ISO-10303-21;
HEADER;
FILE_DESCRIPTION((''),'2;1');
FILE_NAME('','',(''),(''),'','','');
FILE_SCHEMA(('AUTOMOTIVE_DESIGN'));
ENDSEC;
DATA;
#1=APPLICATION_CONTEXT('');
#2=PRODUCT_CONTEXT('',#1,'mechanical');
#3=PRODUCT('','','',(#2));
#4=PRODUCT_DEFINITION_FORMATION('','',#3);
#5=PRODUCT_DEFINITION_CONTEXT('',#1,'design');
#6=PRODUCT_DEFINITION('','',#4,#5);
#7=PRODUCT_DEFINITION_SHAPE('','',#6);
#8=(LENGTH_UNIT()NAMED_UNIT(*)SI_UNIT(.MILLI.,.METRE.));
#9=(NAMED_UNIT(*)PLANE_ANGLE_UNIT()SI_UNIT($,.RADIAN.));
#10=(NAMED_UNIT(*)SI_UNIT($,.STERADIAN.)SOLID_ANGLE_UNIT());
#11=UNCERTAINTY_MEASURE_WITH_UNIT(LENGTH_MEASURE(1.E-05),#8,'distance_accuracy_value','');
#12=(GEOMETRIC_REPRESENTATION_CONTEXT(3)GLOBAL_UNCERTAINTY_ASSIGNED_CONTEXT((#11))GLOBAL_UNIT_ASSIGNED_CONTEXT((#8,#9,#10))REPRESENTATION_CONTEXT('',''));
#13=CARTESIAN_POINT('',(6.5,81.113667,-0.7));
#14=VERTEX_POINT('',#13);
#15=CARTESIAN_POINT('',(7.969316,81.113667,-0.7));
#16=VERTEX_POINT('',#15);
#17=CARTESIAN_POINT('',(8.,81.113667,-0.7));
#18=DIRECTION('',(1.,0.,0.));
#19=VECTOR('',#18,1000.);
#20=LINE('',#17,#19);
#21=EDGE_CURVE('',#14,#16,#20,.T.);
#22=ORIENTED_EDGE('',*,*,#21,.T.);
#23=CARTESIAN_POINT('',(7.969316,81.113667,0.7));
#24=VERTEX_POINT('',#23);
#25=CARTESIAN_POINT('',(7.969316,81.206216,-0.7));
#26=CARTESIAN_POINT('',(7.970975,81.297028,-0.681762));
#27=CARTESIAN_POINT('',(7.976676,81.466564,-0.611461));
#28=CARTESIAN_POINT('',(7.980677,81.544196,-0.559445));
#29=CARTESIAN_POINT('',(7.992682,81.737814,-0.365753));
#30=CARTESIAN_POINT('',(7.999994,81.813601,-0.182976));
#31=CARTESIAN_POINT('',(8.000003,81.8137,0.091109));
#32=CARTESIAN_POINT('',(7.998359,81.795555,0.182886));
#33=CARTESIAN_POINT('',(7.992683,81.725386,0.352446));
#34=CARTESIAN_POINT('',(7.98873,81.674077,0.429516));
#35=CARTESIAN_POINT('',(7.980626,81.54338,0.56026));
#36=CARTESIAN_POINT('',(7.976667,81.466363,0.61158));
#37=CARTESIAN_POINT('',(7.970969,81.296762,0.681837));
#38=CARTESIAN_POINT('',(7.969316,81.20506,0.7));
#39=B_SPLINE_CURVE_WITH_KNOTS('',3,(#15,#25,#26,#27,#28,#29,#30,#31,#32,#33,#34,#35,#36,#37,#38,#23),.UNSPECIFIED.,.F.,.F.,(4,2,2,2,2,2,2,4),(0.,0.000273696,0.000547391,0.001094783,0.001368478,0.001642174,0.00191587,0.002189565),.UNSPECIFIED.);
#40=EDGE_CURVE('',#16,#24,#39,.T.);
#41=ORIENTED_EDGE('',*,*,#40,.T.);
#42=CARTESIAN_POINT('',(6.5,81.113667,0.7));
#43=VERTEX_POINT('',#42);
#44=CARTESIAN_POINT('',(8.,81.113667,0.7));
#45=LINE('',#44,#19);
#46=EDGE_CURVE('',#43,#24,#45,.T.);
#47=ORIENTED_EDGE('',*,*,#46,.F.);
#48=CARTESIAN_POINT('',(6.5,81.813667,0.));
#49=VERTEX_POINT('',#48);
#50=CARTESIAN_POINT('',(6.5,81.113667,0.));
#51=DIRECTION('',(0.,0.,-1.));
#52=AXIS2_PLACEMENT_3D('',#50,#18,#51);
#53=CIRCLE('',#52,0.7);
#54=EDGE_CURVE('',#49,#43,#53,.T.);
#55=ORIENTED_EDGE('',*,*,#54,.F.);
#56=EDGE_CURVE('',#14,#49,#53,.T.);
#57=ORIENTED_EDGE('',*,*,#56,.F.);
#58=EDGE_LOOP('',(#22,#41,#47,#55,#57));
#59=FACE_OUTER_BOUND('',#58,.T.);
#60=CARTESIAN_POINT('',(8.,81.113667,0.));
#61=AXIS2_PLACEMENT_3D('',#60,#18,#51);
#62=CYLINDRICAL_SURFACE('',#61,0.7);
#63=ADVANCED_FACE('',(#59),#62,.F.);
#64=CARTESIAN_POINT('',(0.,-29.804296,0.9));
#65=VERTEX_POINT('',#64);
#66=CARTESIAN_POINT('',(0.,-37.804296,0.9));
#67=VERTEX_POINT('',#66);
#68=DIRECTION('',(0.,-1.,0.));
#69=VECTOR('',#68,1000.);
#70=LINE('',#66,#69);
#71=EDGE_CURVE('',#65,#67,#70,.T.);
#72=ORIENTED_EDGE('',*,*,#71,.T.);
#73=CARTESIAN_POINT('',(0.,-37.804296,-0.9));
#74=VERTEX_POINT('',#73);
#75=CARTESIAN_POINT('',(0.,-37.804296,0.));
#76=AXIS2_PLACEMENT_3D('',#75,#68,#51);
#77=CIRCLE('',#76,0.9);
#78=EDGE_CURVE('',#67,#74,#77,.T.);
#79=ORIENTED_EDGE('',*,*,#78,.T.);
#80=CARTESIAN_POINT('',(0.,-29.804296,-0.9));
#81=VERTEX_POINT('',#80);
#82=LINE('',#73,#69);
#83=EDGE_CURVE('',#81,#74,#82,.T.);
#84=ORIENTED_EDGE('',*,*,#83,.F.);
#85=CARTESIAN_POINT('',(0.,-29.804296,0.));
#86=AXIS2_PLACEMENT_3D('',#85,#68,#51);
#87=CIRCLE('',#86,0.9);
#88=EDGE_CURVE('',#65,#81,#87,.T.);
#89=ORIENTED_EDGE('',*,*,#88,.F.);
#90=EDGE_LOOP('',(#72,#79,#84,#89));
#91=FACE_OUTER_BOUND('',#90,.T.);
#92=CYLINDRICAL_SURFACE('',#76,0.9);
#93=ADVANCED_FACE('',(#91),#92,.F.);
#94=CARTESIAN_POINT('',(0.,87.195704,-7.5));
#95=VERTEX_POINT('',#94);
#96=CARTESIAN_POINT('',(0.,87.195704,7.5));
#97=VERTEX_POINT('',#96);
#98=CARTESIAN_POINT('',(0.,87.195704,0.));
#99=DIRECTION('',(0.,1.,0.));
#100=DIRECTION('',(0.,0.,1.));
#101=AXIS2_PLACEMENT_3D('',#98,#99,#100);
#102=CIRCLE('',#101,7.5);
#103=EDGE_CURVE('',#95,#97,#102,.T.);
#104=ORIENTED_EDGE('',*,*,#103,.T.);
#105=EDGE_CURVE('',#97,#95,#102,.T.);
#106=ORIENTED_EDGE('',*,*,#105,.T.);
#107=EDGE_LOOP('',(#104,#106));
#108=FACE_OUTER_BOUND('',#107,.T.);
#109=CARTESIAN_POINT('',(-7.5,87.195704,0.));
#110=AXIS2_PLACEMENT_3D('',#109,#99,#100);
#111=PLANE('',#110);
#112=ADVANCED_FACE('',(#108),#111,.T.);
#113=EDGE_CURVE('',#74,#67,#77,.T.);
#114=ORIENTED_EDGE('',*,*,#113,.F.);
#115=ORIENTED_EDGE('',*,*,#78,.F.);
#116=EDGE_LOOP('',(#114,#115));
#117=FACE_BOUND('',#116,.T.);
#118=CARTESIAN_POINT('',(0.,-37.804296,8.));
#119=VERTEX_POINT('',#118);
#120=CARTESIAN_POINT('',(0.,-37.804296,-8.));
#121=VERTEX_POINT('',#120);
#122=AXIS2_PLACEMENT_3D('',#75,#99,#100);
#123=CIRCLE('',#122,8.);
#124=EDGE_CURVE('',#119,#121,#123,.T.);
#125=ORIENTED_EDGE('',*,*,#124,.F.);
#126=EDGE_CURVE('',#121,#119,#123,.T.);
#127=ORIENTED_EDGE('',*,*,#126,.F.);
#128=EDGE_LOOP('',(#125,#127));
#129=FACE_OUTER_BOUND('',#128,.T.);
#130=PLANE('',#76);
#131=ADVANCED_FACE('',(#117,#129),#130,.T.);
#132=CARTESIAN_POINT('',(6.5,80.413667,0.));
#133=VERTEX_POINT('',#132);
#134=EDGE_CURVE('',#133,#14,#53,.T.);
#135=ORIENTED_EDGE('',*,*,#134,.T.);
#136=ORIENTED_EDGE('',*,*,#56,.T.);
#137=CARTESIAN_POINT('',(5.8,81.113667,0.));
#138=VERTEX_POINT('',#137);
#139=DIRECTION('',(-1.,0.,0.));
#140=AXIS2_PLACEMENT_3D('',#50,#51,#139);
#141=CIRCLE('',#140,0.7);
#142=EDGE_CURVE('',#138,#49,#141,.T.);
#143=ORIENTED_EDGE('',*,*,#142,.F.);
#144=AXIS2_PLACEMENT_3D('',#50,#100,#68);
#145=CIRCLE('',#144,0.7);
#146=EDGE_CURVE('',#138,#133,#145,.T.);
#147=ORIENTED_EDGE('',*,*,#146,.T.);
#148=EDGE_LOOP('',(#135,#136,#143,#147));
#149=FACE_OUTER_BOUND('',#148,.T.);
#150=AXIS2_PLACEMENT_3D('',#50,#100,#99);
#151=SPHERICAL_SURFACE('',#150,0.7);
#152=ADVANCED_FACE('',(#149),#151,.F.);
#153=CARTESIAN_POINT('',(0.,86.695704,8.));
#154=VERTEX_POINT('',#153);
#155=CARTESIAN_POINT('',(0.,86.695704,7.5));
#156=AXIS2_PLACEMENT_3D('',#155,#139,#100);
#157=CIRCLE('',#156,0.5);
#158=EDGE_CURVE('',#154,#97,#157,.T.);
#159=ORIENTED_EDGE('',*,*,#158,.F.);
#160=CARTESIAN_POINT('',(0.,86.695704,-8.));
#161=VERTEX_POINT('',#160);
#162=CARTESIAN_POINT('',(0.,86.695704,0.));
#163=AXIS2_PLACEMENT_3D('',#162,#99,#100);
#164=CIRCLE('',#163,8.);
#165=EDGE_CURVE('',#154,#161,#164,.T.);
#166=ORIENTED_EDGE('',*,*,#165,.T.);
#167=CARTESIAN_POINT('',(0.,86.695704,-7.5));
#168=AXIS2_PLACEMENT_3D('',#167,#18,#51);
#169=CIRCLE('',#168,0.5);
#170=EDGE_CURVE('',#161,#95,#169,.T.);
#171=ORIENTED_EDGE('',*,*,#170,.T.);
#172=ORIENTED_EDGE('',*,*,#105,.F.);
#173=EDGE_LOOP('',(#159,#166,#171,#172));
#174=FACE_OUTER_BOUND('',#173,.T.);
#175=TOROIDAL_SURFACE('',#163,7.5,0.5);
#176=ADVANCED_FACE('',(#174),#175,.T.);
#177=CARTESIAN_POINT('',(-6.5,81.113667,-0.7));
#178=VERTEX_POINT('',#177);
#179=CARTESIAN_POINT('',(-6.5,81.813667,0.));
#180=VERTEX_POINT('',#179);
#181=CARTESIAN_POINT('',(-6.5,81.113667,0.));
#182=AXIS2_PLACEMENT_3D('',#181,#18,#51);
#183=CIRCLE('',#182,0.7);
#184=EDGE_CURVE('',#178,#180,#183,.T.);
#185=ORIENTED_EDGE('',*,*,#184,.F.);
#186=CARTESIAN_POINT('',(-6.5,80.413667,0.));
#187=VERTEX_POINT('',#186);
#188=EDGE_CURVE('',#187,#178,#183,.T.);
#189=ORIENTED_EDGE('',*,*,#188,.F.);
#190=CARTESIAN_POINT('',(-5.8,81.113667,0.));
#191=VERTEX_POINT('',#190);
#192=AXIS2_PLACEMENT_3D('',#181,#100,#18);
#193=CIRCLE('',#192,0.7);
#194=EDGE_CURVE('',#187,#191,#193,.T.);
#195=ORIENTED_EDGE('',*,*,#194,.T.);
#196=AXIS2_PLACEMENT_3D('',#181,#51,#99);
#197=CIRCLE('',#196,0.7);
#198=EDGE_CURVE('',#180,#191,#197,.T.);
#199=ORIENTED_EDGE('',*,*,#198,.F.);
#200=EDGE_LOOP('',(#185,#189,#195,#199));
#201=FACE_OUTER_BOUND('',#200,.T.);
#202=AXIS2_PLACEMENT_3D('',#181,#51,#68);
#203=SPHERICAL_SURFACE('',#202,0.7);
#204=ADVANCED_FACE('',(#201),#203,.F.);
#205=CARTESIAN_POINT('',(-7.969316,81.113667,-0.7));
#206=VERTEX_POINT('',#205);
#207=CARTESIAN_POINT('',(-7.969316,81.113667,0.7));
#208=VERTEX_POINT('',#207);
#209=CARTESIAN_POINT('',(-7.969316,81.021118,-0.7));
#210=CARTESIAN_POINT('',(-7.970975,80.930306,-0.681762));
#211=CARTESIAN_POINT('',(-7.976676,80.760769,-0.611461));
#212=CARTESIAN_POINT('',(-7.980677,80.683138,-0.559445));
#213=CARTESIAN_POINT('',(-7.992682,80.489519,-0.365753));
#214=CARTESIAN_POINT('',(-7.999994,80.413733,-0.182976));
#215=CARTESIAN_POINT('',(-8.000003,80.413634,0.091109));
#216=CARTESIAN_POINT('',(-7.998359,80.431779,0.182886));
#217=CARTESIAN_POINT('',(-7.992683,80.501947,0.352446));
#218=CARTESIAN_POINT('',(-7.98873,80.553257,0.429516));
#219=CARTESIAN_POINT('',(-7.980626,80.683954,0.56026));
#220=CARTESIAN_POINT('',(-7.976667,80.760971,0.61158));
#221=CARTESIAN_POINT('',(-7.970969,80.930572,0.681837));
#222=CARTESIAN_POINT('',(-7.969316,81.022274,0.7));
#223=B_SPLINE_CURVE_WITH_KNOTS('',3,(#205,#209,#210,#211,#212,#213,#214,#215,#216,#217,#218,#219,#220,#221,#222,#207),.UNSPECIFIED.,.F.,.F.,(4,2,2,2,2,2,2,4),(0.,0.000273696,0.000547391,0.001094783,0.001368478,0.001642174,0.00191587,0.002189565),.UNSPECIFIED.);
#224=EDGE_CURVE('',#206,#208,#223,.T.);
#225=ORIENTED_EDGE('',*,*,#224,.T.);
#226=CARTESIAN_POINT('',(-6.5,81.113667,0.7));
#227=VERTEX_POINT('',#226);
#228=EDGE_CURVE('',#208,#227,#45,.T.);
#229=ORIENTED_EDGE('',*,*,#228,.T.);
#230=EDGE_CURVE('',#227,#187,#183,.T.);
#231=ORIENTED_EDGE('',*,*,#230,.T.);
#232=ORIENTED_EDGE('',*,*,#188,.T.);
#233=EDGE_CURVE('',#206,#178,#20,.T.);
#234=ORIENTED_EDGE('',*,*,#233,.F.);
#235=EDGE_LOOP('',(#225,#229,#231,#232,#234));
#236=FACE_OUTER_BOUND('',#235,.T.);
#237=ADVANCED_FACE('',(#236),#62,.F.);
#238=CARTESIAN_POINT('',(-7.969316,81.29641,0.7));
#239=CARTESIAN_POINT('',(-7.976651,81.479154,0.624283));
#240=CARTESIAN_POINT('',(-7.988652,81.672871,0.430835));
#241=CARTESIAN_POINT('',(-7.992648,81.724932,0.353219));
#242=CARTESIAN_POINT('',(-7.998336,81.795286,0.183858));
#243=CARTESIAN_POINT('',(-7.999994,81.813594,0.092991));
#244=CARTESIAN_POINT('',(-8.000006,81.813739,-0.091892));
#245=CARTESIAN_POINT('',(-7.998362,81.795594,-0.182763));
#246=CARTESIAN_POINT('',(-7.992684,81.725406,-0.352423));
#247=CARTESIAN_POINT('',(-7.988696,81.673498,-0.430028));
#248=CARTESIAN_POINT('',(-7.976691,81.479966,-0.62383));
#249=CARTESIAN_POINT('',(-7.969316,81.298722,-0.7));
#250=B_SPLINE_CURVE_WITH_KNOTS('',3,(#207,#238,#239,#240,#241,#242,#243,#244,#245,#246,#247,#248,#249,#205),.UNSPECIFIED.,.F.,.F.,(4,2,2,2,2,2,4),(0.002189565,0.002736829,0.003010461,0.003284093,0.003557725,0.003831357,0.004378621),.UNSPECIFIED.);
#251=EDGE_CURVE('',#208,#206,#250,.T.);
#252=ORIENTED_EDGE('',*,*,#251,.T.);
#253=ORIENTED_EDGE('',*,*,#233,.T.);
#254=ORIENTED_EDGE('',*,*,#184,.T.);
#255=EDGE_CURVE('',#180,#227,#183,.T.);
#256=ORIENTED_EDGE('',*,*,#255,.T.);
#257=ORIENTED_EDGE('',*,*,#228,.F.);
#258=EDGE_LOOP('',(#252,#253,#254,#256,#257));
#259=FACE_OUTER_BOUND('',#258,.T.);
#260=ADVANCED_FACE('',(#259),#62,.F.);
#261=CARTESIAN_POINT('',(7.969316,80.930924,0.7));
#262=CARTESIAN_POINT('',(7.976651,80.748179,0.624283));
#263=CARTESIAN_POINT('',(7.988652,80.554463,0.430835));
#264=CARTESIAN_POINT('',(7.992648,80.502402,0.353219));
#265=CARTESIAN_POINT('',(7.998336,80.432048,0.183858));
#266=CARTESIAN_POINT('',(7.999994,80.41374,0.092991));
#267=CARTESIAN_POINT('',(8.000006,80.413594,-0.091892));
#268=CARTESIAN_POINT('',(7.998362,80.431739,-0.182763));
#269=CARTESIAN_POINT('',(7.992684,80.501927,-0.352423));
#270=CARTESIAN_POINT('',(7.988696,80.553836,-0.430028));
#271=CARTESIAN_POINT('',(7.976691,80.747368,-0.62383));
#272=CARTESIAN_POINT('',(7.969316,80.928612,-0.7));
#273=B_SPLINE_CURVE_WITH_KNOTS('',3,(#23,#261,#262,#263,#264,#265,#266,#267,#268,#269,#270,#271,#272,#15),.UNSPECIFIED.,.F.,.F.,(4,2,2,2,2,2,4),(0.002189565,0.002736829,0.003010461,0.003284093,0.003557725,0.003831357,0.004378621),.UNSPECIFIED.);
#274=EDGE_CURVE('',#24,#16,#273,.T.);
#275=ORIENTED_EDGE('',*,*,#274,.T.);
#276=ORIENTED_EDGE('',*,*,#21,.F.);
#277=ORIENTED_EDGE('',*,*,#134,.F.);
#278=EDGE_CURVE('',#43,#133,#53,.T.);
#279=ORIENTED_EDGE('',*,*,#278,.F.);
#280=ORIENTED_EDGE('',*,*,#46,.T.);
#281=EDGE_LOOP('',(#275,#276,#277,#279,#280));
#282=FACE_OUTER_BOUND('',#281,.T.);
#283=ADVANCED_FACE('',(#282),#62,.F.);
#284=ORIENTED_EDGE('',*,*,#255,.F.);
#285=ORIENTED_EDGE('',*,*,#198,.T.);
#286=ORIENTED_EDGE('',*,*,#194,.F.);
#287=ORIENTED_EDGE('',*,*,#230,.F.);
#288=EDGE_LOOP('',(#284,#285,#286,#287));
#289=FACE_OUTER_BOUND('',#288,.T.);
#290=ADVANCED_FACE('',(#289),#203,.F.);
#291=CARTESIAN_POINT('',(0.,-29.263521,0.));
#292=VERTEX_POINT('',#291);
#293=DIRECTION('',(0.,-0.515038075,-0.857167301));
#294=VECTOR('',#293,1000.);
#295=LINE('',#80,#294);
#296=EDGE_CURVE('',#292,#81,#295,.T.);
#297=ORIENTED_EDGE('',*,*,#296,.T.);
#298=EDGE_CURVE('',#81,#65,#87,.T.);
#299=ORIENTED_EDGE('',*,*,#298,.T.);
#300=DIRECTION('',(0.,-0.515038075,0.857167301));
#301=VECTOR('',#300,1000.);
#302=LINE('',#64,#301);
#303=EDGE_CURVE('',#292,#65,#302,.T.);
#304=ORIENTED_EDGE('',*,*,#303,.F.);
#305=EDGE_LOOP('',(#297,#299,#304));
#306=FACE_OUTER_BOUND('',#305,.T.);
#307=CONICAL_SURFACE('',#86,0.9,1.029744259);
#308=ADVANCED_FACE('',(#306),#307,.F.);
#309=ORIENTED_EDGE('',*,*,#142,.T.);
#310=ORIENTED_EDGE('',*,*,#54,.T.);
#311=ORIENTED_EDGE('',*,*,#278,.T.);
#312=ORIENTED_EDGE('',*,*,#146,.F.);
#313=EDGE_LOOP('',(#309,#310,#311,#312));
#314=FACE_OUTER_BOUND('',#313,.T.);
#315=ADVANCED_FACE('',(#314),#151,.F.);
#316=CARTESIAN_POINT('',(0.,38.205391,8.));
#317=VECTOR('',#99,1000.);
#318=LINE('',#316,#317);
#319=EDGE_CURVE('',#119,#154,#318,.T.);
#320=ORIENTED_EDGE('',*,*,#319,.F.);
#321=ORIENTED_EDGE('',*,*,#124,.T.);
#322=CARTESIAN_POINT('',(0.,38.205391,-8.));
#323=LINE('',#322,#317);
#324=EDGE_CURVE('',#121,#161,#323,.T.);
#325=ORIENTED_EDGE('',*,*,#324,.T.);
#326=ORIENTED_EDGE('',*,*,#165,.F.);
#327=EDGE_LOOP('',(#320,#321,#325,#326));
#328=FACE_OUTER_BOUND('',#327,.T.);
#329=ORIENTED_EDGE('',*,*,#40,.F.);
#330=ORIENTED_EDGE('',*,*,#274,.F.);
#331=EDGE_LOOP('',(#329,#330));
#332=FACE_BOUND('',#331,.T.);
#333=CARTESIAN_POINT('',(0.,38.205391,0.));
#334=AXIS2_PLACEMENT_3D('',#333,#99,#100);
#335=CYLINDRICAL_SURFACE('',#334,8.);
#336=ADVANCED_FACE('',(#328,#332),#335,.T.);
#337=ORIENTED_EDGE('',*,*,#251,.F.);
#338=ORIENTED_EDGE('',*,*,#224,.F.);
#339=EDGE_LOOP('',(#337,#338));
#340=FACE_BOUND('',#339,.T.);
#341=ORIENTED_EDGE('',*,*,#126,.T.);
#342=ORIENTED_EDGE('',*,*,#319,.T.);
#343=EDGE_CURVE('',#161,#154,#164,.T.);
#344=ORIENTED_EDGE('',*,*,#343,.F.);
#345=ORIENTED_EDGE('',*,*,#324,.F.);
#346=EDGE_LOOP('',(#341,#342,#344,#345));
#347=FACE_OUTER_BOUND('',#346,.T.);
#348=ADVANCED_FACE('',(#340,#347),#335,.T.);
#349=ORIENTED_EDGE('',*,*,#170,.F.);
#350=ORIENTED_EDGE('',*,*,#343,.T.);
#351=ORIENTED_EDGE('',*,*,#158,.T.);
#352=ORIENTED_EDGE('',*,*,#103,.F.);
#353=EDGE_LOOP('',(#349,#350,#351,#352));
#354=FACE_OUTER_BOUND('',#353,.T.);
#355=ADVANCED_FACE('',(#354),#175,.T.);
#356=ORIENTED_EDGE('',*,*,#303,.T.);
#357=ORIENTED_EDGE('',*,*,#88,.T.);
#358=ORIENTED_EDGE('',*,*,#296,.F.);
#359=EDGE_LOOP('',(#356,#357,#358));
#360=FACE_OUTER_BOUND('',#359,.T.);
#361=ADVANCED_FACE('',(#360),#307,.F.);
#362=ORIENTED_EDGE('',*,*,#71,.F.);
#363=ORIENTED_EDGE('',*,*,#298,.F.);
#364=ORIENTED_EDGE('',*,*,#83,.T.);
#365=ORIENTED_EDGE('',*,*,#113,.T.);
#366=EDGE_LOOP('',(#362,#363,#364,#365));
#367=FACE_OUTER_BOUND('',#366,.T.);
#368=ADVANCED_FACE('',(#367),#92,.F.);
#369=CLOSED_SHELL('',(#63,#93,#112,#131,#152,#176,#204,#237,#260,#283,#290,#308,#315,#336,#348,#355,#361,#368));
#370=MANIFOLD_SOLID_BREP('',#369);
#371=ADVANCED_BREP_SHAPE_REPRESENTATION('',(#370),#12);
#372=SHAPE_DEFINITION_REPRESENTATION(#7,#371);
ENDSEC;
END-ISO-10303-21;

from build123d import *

# Parameters (mm, degrees)
CLEARANCE_HOLE_FOR_M1_61_D     = 1.8
CLEARANCE_HOLE_FOR_M1_61_DEPTH = 8
CLEARANCE_HOLE_FOR_M1_61_TIP   = 0.540774557


with BuildPart() as part:
    # Sketch1 → Revolution1 (revolve)
    with BuildSketch(Plane.XY, mode=Mode.PRIVATE) as revolution1_sk:
        with BuildLine():
            Line((0, -37.804295719), (-8, -37.804295719))
            Line((-8, -37.804295719), (-8, 86.695704281))
            ThreePointArc((-8, 86.695704281), (-7.853553391, 87.049257672), (-7.5, 87.195704281))
            Line((-7.5, 87.195704281), (0, 87.195704281))
            Line((0, 87.195704281), (0, -37.804295719))
        make_face()
    revolve(revolution1_sk.sketch.rotate(Axis((0, 38.205391481, 0), (0, -1, 0)), 270), axis=Axis((0, 38.205391481, 0), (0, -1, 0)))

    # Sketch2 → Cut-Revolve1 (revolve, cut)
    with BuildSketch(Plane.XY, mode=Mode.PRIVATE) as cut_revolve1_sk:
        with BuildLine():
            Line((8, 81.81366679), (6.5, 81.81366679))
            ThreePointArc((6.5, 81.81366679), (6.005025253, 81.608641537), (5.8, 81.11366679))
            Line((5.8, 81.11366679), (8, 81.11366679))
            Line((8, 81.11366679), (8, 81.81366679))
        make_face()
        with BuildLine():
            Line((-8, 81.11366679), (-8, 81.81366679))
            Line((-8, 81.81366679), (-6.5, 81.81366679))
            ThreePointArc((-6.5, 81.81366679), (-6.005025253, 81.608641537), (-5.8, 81.11366679))
            Line((-5.8, 81.11366679), (-8, 81.11366679))
        make_face()
    revolve(cut_revolve1_sk.sketch.rotate(Axis((8, 81.11366679, 0), (-1, 0, 0)), 90), axis=Axis((8, 81.11366679, 0), (-1, 0, 0)), mode=Mode.SUBTRACT)

    # Clearance hole for M1.61
    with Locations(Plane(origin=(0, -37.804295719, 0), x_dir=(-1, 0, 0), z_dir=(0, -1, 0))):
        with Locations((0, 0)):
            Hole(CLEARANCE_HOLE_FOR_M1_61_D / 2, depth=CLEARANCE_HOLE_FOR_M1_61_DEPTH)
            with Locations((0, 0, -(CLEARANCE_HOLE_FOR_M1_61_DEPTH + CLEARANCE_HOLE_FOR_M1_61_TIP / 2))):  # 118° drill point
                Cone(0, CLEARANCE_HOLE_FOR_M1_61_D / 2, CLEARANCE_HOLE_FOR_M1_61_TIP, mode=Mode.SUBTRACT)


solid = part.part
